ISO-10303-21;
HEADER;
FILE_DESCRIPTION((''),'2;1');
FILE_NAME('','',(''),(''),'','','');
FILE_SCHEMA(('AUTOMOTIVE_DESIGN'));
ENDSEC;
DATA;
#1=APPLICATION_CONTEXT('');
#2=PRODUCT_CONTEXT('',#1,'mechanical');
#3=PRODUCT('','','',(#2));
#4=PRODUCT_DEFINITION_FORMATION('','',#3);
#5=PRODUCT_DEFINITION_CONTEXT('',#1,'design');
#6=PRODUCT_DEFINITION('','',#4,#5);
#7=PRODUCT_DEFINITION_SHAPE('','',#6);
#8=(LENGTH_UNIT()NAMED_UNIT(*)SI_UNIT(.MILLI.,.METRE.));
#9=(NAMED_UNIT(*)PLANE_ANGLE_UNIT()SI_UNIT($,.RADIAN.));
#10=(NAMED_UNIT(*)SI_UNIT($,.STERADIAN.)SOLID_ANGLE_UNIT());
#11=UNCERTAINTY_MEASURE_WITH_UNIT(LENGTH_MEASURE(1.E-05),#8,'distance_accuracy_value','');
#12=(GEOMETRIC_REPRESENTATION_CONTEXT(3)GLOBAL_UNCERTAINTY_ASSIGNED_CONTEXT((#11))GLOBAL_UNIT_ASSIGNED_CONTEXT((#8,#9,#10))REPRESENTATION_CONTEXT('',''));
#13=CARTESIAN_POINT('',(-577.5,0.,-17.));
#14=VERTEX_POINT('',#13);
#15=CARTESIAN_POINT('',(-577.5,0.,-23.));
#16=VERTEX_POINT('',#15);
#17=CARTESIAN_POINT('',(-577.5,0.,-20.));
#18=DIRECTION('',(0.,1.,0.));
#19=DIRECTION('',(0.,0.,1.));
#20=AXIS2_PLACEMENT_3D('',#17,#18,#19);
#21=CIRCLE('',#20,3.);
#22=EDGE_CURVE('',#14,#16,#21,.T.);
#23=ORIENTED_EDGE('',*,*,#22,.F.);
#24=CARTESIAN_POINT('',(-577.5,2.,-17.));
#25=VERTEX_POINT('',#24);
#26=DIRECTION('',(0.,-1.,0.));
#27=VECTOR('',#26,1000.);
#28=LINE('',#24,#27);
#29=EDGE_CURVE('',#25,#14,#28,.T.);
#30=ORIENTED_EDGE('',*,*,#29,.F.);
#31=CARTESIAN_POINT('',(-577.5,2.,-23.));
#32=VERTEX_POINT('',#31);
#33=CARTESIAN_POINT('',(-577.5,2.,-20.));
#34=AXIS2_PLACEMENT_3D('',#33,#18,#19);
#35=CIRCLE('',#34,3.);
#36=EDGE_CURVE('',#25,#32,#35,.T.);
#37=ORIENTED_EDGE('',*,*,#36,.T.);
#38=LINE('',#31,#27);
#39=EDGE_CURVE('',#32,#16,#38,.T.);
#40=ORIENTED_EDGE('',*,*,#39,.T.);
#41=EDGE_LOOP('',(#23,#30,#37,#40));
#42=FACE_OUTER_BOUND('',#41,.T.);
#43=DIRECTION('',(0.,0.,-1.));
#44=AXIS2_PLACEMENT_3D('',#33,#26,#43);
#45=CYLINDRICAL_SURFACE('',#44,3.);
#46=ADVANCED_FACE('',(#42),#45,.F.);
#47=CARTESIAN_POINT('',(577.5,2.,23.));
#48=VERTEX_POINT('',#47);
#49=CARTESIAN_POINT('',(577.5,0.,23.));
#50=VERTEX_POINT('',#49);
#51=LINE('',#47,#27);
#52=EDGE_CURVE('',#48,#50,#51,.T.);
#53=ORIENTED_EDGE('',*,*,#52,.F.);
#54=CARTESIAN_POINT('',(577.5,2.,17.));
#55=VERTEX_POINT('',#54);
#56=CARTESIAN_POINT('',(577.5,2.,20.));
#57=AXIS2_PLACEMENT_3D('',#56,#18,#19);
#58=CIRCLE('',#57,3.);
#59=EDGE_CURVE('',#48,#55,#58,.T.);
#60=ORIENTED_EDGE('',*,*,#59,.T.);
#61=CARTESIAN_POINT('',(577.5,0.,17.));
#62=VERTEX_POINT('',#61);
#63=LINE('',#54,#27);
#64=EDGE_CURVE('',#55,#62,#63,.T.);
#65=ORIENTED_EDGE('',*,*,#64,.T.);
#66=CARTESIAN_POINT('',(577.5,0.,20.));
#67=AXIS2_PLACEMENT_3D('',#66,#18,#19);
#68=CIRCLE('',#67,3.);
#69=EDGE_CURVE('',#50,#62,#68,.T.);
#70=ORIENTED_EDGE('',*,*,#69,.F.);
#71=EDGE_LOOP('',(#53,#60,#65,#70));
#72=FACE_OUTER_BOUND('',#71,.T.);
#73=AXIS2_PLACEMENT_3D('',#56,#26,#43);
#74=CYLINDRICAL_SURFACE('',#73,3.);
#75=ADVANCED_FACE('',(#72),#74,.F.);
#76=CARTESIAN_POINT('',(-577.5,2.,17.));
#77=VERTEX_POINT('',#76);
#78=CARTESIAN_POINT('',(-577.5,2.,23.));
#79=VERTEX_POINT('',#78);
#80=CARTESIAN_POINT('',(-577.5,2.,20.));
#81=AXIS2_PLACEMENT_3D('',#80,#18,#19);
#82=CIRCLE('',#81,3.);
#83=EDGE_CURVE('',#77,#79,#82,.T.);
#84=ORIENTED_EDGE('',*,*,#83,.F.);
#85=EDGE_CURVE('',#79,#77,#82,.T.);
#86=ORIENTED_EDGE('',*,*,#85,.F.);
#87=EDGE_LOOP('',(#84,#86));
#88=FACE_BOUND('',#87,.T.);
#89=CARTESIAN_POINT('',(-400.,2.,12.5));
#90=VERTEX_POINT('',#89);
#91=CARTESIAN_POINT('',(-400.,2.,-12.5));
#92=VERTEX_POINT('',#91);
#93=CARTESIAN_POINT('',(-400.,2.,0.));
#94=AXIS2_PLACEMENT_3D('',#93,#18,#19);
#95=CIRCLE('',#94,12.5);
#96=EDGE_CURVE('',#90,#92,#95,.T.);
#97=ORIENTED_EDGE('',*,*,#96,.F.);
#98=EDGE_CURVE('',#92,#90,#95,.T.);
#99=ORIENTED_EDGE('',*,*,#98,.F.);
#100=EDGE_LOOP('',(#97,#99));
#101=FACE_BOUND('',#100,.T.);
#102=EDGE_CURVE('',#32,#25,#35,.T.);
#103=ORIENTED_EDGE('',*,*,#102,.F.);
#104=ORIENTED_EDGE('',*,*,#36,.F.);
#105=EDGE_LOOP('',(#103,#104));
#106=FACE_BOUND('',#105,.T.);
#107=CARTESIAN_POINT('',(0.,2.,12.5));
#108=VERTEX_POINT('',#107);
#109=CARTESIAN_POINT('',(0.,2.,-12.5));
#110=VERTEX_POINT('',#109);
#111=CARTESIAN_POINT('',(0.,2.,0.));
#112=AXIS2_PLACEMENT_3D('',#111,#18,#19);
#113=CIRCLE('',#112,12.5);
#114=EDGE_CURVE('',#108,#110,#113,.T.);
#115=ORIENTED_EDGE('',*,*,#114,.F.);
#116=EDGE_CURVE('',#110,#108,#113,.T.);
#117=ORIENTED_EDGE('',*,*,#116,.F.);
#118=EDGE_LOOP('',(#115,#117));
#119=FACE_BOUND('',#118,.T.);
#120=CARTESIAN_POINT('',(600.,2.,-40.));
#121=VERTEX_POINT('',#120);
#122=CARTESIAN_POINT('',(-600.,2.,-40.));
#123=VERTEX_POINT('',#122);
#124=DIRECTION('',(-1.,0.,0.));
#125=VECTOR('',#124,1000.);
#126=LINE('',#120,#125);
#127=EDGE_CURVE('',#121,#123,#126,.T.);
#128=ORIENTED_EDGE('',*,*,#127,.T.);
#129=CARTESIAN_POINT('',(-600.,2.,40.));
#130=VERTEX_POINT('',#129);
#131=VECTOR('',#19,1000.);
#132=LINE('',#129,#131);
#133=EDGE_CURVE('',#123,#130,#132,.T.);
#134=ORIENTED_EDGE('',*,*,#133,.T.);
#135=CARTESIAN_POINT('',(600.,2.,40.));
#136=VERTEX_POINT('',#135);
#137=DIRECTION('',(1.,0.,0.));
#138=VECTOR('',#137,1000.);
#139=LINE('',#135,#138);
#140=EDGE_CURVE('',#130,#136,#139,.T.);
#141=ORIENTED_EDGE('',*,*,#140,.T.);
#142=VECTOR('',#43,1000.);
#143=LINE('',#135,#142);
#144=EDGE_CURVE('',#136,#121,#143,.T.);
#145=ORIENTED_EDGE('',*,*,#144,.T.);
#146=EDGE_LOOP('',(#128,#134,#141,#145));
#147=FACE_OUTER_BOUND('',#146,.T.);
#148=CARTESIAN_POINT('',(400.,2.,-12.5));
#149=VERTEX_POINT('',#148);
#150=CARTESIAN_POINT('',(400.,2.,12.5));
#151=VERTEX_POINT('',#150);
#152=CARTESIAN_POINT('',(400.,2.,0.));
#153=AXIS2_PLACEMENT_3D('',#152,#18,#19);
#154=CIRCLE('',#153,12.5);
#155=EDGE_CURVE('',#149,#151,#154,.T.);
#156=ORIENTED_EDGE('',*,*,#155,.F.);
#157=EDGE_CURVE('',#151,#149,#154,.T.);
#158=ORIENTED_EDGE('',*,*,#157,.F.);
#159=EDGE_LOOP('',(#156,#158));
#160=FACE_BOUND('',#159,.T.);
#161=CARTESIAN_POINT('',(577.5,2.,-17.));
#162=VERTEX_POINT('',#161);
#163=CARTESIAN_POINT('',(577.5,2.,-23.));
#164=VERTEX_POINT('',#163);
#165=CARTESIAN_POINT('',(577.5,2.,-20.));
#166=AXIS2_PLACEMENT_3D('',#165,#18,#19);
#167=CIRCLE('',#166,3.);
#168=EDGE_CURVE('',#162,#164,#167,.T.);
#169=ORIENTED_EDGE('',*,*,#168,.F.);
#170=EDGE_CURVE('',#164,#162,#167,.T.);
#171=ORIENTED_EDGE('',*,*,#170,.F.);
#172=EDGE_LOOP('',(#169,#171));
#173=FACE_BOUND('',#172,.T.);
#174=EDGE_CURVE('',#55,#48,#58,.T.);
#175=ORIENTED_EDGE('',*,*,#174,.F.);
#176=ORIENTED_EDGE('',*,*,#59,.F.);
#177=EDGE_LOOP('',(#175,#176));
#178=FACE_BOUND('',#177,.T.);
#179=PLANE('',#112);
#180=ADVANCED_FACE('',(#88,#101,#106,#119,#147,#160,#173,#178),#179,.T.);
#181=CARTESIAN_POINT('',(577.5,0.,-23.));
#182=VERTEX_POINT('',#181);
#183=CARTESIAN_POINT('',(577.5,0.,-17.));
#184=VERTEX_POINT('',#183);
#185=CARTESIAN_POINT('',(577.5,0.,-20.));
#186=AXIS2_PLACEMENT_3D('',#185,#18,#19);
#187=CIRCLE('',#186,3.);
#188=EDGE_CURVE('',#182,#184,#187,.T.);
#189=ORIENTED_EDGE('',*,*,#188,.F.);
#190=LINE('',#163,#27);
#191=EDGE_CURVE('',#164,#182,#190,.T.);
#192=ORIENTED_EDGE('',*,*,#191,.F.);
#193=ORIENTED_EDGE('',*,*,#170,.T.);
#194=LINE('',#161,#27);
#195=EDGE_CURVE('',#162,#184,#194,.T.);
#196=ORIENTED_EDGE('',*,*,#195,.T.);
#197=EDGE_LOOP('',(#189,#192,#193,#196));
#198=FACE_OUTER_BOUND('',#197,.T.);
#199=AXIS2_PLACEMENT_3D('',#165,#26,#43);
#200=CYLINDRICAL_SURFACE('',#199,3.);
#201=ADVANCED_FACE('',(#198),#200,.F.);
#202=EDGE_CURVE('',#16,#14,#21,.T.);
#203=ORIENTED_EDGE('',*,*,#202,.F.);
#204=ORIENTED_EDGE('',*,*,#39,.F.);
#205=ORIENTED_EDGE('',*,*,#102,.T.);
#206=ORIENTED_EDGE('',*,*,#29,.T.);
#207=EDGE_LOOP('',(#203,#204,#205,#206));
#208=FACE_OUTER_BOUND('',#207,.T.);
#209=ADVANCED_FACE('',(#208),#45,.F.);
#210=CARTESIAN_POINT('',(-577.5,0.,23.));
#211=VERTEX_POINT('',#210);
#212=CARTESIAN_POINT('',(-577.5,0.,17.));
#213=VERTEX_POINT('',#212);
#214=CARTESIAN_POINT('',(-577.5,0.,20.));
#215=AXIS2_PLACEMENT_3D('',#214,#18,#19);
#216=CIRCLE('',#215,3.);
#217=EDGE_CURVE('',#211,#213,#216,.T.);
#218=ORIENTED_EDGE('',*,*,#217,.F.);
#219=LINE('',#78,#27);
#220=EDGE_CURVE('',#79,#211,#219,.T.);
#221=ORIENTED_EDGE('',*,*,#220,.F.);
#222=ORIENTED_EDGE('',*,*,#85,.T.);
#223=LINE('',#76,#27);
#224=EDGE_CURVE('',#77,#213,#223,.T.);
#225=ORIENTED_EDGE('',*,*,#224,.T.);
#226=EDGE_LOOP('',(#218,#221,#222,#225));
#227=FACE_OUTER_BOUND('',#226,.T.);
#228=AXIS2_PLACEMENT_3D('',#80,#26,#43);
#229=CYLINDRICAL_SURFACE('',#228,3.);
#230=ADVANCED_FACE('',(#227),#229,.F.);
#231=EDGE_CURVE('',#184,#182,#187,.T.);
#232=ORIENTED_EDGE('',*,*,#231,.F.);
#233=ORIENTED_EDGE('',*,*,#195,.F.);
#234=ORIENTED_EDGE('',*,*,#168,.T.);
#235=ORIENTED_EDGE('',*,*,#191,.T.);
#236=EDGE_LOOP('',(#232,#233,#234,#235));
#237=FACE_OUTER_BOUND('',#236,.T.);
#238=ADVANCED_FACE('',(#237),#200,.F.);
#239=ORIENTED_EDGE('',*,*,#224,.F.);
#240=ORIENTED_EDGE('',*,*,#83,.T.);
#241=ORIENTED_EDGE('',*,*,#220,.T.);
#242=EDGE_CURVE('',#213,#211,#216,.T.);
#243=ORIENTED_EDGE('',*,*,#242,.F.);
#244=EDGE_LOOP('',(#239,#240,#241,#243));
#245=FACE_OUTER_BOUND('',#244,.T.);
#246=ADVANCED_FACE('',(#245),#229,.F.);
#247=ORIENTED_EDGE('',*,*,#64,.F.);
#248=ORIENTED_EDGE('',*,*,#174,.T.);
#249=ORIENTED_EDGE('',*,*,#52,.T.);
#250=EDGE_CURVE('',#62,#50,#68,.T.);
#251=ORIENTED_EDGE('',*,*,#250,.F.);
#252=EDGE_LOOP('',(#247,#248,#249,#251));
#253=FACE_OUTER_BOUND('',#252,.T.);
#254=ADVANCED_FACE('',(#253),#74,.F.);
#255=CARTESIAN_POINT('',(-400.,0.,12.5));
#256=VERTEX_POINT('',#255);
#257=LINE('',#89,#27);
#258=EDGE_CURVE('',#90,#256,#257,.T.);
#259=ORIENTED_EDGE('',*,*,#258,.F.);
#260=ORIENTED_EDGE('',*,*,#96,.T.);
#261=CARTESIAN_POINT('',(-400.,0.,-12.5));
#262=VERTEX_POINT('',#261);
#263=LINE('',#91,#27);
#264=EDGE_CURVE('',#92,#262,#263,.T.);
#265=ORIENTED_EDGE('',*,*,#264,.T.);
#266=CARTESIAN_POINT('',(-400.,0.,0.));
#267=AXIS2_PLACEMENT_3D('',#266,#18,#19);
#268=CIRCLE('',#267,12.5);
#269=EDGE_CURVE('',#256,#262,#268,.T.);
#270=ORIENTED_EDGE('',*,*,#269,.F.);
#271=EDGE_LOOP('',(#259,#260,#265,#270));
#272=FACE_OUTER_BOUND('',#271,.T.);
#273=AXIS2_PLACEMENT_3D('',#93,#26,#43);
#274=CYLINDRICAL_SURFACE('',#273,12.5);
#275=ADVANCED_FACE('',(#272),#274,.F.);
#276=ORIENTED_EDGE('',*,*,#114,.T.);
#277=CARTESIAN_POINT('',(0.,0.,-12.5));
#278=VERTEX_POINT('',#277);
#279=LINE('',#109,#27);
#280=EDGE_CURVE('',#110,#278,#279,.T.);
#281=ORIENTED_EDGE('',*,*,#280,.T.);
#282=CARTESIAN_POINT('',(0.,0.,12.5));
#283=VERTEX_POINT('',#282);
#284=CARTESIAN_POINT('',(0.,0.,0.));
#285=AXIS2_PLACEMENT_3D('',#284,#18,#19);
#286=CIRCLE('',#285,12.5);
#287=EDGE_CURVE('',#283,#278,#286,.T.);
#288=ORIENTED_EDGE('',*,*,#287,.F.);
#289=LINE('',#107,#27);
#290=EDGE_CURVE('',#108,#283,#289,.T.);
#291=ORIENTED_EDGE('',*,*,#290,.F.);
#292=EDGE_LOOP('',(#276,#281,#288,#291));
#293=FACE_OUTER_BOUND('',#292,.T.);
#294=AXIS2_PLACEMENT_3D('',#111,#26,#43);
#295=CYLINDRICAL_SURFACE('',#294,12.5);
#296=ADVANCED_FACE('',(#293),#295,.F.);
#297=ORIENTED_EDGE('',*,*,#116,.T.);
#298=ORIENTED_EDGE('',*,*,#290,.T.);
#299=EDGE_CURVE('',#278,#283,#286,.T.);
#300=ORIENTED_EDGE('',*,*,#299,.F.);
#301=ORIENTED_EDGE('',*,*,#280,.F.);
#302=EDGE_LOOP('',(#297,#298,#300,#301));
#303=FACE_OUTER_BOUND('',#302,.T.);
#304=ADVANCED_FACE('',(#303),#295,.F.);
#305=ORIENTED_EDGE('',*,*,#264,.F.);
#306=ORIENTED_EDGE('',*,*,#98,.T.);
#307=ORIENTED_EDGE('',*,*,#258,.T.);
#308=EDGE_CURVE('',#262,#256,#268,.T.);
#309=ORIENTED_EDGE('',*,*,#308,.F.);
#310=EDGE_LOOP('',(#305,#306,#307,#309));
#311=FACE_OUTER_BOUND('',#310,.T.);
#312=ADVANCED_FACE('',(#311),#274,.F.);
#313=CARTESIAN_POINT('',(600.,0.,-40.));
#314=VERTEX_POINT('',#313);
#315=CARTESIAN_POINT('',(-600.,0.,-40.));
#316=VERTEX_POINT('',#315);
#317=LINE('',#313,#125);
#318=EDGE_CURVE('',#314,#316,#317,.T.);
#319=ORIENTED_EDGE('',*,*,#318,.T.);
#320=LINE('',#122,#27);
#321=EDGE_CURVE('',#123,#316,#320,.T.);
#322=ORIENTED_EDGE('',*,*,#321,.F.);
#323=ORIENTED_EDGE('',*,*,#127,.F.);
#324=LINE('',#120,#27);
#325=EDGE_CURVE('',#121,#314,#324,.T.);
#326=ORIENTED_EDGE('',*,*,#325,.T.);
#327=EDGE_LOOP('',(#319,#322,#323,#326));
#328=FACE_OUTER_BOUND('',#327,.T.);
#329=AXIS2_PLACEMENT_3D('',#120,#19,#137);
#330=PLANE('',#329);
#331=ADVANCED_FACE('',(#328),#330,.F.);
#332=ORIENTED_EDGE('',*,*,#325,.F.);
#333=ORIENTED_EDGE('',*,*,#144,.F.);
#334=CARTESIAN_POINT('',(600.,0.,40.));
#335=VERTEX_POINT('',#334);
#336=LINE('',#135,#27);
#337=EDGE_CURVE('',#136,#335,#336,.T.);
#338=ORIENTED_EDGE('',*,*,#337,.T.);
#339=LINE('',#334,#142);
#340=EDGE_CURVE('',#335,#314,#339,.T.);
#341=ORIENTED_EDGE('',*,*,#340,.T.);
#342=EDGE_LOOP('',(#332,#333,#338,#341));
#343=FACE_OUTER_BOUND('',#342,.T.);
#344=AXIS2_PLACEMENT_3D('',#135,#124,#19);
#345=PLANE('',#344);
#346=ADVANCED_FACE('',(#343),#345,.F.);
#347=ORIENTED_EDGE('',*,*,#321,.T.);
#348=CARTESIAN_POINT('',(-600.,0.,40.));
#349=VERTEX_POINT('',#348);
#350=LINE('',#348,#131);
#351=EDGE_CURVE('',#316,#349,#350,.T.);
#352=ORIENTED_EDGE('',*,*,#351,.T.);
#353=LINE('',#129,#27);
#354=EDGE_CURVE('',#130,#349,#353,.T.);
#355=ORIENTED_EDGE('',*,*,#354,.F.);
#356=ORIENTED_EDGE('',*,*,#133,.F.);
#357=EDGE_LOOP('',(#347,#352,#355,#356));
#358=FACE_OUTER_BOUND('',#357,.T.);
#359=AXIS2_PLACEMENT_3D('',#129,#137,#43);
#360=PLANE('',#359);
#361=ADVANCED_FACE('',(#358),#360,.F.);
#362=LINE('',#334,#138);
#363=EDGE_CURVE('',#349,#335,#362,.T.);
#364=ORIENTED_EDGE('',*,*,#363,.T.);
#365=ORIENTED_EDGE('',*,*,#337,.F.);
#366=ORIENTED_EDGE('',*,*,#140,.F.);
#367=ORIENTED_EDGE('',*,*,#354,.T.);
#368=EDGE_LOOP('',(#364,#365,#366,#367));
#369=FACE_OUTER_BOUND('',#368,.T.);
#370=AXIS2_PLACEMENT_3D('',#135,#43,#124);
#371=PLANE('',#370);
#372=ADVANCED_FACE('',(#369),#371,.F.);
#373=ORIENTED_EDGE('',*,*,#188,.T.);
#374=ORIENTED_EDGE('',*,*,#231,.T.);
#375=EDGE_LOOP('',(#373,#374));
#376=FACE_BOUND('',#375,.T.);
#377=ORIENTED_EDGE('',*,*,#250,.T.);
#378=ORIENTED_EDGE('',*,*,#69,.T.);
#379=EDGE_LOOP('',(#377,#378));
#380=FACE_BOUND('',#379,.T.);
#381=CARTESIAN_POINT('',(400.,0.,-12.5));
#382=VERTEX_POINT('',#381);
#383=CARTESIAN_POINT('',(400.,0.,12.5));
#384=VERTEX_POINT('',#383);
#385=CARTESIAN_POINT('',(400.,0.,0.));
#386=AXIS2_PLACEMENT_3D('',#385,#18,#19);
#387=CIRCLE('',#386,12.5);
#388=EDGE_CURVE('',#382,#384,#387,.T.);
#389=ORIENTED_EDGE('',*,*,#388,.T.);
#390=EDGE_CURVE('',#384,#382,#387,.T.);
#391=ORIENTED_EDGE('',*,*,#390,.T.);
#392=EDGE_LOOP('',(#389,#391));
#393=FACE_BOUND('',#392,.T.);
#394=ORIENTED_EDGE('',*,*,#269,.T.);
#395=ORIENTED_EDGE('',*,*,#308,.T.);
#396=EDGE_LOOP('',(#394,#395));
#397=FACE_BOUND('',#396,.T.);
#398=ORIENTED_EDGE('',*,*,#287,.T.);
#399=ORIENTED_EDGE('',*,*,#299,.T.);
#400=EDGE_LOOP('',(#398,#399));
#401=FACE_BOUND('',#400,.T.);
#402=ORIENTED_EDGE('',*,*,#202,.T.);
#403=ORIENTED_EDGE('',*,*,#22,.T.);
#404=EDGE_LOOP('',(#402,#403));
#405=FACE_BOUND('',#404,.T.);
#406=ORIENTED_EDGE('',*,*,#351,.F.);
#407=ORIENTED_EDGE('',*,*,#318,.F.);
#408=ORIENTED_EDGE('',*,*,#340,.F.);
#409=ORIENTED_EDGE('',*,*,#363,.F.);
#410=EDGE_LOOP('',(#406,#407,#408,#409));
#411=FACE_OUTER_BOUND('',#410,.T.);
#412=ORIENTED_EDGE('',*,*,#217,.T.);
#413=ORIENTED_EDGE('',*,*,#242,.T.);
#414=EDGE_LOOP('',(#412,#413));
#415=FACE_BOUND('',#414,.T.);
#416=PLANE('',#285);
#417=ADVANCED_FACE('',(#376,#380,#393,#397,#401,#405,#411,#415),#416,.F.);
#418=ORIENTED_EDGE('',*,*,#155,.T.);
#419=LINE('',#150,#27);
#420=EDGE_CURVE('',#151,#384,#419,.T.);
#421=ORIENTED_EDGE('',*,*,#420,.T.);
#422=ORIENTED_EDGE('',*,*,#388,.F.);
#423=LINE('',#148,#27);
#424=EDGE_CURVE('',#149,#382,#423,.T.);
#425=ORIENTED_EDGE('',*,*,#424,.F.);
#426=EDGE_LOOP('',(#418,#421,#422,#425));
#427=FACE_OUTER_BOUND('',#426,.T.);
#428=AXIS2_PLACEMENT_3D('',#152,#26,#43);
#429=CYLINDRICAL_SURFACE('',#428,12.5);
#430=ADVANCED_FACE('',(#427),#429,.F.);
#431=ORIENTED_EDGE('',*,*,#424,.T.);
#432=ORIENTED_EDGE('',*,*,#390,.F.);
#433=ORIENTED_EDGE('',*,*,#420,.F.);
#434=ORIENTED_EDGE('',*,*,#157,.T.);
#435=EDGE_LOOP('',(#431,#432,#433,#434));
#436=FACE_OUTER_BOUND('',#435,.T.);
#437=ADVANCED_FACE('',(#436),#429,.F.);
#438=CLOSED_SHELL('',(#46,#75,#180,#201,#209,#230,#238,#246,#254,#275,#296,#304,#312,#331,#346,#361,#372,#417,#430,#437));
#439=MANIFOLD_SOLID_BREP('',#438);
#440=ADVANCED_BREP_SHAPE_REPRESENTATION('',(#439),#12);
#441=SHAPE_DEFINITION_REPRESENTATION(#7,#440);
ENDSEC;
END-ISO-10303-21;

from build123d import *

# Parameters (mm, degrees)
SKETCH1_W           = 1200
SKETCH1_H           = 80
SKETCH1_R           = 12.5
SKETCH1_R_2         = 3
BOSS_EXTRUDE1_DEPTH = 2


with BuildPart() as part:
    # Sketch1 → Boss-Extrude1 (new body)
    with BuildSketch(Plane(origin=(0, 0, 0), x_dir=(1, 0, 0), z_dir=(0, 1, 0))):
        Rectangle(SKETCH1_W, SKETCH1_H)
        with Locations(Location((-400, 0, 0), (0, 0, 270))):
            Circle(SKETCH1_R, mode=Mode.SUBTRACT)
        with Locations(Location((400, 0, 0), (0, 0, 270))):
            Circle(SKETCH1_R, mode=Mode.SUBTRACT)
        with Locations(Location((-577.5, 20, 0), (0, 0, 270))):
            Circle(SKETCH1_R_2, mode=Mode.SUBTRACT)
        with Locations(Location((577.5, 20, 0), (0, 0, 270))):
            Circle(SKETCH1_R_2, mode=Mode.SUBTRACT)
        with Locations(Location((-577.5, -20, 0), (0, 0, 270))):
            Circle(SKETCH1_R_2, mode=Mode.SUBTRACT)
        with Locations(Location((577.5, -20, 0), (0, 0, 270))):
            Circle(SKETCH1_R_2, mode=Mode.SUBTRACT)
        with Locations(Location((0, 0, 0), (0, 0, 270))):
            Circle(SKETCH1_R, mode=Mode.SUBTRACT)
    extrude(amount=BOSS_EXTRUDE1_DEPTH)


solid = part.part
